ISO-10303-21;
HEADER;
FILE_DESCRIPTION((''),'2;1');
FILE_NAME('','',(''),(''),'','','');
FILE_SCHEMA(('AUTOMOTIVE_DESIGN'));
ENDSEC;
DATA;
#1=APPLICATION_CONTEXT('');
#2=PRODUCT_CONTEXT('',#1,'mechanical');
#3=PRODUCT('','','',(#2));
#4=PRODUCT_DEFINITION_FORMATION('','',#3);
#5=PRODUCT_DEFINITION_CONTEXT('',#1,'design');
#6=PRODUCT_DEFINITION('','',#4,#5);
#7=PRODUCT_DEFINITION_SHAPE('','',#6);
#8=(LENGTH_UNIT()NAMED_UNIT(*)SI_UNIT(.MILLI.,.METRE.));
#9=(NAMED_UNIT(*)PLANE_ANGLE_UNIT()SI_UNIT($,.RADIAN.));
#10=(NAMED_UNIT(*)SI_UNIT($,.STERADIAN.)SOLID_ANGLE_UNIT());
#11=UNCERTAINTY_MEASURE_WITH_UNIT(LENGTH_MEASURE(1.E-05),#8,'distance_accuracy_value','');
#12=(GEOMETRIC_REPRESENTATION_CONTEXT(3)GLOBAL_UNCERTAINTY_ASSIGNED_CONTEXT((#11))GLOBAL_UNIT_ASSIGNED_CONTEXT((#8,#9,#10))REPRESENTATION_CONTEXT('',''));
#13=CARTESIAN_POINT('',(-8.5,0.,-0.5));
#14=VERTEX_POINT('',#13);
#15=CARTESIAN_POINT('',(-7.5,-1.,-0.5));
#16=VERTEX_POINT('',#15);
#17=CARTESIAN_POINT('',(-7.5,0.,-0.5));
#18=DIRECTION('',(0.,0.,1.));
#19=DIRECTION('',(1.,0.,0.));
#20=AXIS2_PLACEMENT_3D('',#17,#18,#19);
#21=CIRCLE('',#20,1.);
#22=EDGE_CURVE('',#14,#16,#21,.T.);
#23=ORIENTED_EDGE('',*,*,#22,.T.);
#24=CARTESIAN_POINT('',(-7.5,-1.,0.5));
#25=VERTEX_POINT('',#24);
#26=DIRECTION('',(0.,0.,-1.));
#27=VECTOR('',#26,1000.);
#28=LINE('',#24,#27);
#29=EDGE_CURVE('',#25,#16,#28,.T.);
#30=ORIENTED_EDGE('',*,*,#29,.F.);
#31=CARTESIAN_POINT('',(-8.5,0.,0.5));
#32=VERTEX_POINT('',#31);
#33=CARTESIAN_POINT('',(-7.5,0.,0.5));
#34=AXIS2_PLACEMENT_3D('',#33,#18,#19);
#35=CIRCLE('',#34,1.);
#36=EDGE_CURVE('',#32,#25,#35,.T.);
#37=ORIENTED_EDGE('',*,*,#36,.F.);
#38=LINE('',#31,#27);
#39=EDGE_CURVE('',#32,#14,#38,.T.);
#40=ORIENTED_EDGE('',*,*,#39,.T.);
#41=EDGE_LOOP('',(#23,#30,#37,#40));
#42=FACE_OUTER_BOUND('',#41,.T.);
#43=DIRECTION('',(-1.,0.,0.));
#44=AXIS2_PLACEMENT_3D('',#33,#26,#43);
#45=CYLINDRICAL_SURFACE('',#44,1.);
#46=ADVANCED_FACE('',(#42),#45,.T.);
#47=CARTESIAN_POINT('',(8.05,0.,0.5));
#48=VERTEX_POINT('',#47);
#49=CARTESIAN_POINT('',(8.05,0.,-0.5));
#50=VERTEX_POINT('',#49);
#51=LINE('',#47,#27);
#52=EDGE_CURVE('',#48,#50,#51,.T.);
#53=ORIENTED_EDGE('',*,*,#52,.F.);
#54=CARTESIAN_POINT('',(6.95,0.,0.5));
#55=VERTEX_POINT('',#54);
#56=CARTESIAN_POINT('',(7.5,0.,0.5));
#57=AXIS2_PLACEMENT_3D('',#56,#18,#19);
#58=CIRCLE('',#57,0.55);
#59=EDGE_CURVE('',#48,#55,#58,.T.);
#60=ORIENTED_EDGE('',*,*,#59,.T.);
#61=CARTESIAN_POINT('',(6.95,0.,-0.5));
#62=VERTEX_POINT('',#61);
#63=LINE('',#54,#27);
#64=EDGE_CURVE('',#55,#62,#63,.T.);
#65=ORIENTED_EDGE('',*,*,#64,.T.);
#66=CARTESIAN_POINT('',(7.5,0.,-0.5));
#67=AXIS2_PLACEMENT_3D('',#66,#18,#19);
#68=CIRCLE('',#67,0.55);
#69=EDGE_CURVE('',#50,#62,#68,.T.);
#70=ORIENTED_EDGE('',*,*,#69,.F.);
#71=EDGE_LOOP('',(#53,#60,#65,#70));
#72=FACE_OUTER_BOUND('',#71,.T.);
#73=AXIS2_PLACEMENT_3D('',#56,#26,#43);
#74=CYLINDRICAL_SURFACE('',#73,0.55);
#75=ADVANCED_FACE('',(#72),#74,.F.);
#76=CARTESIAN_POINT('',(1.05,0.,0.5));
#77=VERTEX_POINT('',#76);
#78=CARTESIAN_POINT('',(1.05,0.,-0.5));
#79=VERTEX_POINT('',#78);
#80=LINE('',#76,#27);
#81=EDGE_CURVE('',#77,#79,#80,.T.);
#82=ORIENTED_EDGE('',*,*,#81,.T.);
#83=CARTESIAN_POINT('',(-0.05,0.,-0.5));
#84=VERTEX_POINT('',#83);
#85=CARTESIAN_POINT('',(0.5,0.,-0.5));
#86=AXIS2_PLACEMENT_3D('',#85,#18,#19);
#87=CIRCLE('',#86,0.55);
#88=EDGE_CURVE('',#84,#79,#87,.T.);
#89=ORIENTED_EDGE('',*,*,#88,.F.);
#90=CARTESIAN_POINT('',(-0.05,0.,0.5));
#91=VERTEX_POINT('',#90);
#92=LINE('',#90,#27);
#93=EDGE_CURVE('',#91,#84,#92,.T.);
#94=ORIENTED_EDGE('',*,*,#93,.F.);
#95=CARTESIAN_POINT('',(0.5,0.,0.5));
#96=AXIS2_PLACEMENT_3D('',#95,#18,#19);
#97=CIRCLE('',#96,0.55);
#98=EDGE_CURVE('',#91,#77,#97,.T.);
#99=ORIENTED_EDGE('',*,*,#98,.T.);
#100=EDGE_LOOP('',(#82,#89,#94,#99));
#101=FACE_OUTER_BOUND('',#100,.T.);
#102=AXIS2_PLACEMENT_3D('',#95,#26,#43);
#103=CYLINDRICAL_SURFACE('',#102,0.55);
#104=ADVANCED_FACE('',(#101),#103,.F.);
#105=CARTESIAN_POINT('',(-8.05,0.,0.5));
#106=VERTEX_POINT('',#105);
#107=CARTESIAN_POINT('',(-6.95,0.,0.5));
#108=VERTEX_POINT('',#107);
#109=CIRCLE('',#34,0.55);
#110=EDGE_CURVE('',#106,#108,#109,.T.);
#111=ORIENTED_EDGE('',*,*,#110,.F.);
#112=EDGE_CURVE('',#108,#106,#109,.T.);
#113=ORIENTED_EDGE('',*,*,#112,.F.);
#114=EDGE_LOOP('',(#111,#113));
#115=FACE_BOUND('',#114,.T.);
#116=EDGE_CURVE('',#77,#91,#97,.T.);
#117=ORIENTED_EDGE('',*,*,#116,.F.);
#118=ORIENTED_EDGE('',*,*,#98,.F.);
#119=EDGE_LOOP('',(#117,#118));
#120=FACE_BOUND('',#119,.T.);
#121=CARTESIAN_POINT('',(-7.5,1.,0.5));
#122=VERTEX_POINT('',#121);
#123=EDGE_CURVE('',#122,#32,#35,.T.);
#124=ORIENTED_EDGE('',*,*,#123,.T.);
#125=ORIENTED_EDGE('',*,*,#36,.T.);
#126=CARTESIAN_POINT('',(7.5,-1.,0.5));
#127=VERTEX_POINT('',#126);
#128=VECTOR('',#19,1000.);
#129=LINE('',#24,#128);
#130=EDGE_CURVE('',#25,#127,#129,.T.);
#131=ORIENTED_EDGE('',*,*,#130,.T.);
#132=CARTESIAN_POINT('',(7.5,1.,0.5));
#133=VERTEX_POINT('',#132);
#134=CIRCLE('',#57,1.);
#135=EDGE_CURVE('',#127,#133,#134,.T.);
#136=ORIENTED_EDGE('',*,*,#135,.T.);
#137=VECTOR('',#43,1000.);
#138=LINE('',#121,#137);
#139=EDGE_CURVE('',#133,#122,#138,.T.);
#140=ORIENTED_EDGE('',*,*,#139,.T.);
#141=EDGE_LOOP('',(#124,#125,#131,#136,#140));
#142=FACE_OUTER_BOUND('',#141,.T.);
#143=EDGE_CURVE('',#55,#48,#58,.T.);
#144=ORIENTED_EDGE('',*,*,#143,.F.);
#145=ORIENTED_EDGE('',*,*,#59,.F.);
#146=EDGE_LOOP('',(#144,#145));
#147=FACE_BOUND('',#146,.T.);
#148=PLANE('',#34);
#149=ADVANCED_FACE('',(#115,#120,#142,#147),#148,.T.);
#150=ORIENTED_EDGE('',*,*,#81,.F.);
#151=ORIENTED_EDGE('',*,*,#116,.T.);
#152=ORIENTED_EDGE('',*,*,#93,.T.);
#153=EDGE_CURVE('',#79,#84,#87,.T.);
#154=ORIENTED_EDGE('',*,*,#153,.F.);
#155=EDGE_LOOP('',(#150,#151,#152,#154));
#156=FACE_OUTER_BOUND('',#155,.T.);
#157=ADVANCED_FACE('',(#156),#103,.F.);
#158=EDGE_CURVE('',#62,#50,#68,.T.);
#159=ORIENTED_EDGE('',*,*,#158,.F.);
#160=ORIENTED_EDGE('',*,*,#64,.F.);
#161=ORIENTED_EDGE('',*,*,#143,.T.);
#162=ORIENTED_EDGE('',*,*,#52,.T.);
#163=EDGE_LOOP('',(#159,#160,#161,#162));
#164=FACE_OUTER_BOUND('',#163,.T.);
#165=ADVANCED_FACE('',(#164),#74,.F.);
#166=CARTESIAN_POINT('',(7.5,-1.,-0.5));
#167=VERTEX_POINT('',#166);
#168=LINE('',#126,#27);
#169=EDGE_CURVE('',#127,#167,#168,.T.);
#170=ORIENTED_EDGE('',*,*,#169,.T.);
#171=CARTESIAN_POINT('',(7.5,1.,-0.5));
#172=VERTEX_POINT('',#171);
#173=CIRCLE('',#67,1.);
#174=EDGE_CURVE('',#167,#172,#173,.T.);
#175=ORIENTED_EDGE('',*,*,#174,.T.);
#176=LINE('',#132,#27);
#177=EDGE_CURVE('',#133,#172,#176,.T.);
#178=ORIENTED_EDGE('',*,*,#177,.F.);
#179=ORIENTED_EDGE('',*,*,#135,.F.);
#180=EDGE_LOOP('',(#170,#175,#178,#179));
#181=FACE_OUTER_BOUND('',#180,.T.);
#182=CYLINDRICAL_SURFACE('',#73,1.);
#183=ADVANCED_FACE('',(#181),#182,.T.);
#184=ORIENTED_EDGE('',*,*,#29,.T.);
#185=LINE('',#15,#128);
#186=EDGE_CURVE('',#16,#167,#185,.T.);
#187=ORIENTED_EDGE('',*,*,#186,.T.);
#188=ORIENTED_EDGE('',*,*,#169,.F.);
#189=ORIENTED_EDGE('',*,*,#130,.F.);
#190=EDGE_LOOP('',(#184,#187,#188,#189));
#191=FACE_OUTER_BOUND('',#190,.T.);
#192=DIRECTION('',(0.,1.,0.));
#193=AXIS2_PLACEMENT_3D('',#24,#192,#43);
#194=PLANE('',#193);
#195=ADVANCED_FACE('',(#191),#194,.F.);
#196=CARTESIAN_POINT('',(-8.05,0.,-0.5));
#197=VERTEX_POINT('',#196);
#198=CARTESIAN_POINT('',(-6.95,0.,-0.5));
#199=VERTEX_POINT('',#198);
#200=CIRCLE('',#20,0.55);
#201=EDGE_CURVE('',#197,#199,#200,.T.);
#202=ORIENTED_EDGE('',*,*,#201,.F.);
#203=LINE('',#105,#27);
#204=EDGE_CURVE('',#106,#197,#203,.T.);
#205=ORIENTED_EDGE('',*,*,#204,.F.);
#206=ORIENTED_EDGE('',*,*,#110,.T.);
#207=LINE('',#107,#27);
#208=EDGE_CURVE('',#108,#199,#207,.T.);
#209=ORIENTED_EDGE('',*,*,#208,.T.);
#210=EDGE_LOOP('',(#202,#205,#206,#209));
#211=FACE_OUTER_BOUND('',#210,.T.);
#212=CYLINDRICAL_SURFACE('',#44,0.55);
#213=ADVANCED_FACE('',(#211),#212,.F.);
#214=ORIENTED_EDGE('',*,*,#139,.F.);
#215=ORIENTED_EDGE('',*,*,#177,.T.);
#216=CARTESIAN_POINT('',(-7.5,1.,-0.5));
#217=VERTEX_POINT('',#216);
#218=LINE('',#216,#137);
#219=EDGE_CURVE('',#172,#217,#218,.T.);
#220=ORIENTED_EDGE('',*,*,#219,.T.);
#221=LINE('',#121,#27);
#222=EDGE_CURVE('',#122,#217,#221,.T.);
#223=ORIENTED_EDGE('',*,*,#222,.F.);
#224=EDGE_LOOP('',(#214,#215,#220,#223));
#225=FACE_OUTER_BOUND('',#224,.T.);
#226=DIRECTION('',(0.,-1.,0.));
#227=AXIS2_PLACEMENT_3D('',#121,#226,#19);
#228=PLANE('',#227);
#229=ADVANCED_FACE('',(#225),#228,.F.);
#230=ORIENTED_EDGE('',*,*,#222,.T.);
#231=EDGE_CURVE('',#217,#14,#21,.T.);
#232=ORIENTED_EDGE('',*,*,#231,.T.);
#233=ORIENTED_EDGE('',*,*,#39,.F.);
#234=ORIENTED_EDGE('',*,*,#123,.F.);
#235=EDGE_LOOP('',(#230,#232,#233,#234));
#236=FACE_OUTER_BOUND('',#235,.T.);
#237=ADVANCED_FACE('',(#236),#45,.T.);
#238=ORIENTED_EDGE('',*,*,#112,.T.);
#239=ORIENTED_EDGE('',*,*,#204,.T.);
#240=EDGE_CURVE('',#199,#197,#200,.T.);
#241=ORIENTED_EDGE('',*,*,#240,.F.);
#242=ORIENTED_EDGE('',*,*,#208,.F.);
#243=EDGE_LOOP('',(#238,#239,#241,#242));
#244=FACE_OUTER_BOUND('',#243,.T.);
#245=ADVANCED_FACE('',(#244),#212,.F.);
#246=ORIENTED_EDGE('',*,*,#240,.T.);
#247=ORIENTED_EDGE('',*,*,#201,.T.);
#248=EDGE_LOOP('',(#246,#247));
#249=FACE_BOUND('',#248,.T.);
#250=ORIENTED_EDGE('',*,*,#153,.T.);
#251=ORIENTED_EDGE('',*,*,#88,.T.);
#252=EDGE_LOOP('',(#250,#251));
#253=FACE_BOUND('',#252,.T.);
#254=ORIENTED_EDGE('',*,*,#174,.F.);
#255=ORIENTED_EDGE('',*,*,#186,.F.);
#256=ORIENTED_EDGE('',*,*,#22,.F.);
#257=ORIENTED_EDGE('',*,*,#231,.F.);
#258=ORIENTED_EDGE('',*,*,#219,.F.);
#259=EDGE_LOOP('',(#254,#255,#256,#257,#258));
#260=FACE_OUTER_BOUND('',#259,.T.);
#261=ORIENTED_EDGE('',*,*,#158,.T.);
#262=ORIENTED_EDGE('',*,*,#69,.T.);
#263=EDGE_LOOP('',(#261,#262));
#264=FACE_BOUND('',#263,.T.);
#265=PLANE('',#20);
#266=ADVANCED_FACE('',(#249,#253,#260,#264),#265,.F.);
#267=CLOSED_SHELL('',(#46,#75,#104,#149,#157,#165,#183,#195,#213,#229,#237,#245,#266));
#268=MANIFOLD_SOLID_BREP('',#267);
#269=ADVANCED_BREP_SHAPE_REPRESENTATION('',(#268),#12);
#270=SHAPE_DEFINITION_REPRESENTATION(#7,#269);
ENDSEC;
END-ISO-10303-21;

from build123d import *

# Parameters (mm, degrees)
SKETCH1_R           = 0.55
THIGH1_LENGTH_DEPTH = 0.5


with BuildPart() as part:
    # Sketch1 → Thigh1 length (new, symmetric)
    with BuildSketch(Plane.XY):
        with BuildLine():
            Line((-7.5, 1), (7.5, 1))
            ThreePointArc((7.5, 1), (8.5, 0), (7.5, -1))
            Line((7.5, -1), (-7.5, -1))
            ThreePointArc((-7.5, -1), (-8.5, 0), (-7.5, 1))
        make_face()
        with Locations((-7.5, 0)):
            Circle(SKETCH1_R, mode=Mode.SUBTRACT)
        with Locations((7.5, 0)):
            Circle(SKETCH1_R, mode=Mode.SUBTRACT)
        with Locations((0.5, 0)):
            Circle(SKETCH1_R, mode=Mode.SUBTRACT)
    extrude(amount=THIGH1_LENGTH_DEPTH, both=True)


solid = part.part
